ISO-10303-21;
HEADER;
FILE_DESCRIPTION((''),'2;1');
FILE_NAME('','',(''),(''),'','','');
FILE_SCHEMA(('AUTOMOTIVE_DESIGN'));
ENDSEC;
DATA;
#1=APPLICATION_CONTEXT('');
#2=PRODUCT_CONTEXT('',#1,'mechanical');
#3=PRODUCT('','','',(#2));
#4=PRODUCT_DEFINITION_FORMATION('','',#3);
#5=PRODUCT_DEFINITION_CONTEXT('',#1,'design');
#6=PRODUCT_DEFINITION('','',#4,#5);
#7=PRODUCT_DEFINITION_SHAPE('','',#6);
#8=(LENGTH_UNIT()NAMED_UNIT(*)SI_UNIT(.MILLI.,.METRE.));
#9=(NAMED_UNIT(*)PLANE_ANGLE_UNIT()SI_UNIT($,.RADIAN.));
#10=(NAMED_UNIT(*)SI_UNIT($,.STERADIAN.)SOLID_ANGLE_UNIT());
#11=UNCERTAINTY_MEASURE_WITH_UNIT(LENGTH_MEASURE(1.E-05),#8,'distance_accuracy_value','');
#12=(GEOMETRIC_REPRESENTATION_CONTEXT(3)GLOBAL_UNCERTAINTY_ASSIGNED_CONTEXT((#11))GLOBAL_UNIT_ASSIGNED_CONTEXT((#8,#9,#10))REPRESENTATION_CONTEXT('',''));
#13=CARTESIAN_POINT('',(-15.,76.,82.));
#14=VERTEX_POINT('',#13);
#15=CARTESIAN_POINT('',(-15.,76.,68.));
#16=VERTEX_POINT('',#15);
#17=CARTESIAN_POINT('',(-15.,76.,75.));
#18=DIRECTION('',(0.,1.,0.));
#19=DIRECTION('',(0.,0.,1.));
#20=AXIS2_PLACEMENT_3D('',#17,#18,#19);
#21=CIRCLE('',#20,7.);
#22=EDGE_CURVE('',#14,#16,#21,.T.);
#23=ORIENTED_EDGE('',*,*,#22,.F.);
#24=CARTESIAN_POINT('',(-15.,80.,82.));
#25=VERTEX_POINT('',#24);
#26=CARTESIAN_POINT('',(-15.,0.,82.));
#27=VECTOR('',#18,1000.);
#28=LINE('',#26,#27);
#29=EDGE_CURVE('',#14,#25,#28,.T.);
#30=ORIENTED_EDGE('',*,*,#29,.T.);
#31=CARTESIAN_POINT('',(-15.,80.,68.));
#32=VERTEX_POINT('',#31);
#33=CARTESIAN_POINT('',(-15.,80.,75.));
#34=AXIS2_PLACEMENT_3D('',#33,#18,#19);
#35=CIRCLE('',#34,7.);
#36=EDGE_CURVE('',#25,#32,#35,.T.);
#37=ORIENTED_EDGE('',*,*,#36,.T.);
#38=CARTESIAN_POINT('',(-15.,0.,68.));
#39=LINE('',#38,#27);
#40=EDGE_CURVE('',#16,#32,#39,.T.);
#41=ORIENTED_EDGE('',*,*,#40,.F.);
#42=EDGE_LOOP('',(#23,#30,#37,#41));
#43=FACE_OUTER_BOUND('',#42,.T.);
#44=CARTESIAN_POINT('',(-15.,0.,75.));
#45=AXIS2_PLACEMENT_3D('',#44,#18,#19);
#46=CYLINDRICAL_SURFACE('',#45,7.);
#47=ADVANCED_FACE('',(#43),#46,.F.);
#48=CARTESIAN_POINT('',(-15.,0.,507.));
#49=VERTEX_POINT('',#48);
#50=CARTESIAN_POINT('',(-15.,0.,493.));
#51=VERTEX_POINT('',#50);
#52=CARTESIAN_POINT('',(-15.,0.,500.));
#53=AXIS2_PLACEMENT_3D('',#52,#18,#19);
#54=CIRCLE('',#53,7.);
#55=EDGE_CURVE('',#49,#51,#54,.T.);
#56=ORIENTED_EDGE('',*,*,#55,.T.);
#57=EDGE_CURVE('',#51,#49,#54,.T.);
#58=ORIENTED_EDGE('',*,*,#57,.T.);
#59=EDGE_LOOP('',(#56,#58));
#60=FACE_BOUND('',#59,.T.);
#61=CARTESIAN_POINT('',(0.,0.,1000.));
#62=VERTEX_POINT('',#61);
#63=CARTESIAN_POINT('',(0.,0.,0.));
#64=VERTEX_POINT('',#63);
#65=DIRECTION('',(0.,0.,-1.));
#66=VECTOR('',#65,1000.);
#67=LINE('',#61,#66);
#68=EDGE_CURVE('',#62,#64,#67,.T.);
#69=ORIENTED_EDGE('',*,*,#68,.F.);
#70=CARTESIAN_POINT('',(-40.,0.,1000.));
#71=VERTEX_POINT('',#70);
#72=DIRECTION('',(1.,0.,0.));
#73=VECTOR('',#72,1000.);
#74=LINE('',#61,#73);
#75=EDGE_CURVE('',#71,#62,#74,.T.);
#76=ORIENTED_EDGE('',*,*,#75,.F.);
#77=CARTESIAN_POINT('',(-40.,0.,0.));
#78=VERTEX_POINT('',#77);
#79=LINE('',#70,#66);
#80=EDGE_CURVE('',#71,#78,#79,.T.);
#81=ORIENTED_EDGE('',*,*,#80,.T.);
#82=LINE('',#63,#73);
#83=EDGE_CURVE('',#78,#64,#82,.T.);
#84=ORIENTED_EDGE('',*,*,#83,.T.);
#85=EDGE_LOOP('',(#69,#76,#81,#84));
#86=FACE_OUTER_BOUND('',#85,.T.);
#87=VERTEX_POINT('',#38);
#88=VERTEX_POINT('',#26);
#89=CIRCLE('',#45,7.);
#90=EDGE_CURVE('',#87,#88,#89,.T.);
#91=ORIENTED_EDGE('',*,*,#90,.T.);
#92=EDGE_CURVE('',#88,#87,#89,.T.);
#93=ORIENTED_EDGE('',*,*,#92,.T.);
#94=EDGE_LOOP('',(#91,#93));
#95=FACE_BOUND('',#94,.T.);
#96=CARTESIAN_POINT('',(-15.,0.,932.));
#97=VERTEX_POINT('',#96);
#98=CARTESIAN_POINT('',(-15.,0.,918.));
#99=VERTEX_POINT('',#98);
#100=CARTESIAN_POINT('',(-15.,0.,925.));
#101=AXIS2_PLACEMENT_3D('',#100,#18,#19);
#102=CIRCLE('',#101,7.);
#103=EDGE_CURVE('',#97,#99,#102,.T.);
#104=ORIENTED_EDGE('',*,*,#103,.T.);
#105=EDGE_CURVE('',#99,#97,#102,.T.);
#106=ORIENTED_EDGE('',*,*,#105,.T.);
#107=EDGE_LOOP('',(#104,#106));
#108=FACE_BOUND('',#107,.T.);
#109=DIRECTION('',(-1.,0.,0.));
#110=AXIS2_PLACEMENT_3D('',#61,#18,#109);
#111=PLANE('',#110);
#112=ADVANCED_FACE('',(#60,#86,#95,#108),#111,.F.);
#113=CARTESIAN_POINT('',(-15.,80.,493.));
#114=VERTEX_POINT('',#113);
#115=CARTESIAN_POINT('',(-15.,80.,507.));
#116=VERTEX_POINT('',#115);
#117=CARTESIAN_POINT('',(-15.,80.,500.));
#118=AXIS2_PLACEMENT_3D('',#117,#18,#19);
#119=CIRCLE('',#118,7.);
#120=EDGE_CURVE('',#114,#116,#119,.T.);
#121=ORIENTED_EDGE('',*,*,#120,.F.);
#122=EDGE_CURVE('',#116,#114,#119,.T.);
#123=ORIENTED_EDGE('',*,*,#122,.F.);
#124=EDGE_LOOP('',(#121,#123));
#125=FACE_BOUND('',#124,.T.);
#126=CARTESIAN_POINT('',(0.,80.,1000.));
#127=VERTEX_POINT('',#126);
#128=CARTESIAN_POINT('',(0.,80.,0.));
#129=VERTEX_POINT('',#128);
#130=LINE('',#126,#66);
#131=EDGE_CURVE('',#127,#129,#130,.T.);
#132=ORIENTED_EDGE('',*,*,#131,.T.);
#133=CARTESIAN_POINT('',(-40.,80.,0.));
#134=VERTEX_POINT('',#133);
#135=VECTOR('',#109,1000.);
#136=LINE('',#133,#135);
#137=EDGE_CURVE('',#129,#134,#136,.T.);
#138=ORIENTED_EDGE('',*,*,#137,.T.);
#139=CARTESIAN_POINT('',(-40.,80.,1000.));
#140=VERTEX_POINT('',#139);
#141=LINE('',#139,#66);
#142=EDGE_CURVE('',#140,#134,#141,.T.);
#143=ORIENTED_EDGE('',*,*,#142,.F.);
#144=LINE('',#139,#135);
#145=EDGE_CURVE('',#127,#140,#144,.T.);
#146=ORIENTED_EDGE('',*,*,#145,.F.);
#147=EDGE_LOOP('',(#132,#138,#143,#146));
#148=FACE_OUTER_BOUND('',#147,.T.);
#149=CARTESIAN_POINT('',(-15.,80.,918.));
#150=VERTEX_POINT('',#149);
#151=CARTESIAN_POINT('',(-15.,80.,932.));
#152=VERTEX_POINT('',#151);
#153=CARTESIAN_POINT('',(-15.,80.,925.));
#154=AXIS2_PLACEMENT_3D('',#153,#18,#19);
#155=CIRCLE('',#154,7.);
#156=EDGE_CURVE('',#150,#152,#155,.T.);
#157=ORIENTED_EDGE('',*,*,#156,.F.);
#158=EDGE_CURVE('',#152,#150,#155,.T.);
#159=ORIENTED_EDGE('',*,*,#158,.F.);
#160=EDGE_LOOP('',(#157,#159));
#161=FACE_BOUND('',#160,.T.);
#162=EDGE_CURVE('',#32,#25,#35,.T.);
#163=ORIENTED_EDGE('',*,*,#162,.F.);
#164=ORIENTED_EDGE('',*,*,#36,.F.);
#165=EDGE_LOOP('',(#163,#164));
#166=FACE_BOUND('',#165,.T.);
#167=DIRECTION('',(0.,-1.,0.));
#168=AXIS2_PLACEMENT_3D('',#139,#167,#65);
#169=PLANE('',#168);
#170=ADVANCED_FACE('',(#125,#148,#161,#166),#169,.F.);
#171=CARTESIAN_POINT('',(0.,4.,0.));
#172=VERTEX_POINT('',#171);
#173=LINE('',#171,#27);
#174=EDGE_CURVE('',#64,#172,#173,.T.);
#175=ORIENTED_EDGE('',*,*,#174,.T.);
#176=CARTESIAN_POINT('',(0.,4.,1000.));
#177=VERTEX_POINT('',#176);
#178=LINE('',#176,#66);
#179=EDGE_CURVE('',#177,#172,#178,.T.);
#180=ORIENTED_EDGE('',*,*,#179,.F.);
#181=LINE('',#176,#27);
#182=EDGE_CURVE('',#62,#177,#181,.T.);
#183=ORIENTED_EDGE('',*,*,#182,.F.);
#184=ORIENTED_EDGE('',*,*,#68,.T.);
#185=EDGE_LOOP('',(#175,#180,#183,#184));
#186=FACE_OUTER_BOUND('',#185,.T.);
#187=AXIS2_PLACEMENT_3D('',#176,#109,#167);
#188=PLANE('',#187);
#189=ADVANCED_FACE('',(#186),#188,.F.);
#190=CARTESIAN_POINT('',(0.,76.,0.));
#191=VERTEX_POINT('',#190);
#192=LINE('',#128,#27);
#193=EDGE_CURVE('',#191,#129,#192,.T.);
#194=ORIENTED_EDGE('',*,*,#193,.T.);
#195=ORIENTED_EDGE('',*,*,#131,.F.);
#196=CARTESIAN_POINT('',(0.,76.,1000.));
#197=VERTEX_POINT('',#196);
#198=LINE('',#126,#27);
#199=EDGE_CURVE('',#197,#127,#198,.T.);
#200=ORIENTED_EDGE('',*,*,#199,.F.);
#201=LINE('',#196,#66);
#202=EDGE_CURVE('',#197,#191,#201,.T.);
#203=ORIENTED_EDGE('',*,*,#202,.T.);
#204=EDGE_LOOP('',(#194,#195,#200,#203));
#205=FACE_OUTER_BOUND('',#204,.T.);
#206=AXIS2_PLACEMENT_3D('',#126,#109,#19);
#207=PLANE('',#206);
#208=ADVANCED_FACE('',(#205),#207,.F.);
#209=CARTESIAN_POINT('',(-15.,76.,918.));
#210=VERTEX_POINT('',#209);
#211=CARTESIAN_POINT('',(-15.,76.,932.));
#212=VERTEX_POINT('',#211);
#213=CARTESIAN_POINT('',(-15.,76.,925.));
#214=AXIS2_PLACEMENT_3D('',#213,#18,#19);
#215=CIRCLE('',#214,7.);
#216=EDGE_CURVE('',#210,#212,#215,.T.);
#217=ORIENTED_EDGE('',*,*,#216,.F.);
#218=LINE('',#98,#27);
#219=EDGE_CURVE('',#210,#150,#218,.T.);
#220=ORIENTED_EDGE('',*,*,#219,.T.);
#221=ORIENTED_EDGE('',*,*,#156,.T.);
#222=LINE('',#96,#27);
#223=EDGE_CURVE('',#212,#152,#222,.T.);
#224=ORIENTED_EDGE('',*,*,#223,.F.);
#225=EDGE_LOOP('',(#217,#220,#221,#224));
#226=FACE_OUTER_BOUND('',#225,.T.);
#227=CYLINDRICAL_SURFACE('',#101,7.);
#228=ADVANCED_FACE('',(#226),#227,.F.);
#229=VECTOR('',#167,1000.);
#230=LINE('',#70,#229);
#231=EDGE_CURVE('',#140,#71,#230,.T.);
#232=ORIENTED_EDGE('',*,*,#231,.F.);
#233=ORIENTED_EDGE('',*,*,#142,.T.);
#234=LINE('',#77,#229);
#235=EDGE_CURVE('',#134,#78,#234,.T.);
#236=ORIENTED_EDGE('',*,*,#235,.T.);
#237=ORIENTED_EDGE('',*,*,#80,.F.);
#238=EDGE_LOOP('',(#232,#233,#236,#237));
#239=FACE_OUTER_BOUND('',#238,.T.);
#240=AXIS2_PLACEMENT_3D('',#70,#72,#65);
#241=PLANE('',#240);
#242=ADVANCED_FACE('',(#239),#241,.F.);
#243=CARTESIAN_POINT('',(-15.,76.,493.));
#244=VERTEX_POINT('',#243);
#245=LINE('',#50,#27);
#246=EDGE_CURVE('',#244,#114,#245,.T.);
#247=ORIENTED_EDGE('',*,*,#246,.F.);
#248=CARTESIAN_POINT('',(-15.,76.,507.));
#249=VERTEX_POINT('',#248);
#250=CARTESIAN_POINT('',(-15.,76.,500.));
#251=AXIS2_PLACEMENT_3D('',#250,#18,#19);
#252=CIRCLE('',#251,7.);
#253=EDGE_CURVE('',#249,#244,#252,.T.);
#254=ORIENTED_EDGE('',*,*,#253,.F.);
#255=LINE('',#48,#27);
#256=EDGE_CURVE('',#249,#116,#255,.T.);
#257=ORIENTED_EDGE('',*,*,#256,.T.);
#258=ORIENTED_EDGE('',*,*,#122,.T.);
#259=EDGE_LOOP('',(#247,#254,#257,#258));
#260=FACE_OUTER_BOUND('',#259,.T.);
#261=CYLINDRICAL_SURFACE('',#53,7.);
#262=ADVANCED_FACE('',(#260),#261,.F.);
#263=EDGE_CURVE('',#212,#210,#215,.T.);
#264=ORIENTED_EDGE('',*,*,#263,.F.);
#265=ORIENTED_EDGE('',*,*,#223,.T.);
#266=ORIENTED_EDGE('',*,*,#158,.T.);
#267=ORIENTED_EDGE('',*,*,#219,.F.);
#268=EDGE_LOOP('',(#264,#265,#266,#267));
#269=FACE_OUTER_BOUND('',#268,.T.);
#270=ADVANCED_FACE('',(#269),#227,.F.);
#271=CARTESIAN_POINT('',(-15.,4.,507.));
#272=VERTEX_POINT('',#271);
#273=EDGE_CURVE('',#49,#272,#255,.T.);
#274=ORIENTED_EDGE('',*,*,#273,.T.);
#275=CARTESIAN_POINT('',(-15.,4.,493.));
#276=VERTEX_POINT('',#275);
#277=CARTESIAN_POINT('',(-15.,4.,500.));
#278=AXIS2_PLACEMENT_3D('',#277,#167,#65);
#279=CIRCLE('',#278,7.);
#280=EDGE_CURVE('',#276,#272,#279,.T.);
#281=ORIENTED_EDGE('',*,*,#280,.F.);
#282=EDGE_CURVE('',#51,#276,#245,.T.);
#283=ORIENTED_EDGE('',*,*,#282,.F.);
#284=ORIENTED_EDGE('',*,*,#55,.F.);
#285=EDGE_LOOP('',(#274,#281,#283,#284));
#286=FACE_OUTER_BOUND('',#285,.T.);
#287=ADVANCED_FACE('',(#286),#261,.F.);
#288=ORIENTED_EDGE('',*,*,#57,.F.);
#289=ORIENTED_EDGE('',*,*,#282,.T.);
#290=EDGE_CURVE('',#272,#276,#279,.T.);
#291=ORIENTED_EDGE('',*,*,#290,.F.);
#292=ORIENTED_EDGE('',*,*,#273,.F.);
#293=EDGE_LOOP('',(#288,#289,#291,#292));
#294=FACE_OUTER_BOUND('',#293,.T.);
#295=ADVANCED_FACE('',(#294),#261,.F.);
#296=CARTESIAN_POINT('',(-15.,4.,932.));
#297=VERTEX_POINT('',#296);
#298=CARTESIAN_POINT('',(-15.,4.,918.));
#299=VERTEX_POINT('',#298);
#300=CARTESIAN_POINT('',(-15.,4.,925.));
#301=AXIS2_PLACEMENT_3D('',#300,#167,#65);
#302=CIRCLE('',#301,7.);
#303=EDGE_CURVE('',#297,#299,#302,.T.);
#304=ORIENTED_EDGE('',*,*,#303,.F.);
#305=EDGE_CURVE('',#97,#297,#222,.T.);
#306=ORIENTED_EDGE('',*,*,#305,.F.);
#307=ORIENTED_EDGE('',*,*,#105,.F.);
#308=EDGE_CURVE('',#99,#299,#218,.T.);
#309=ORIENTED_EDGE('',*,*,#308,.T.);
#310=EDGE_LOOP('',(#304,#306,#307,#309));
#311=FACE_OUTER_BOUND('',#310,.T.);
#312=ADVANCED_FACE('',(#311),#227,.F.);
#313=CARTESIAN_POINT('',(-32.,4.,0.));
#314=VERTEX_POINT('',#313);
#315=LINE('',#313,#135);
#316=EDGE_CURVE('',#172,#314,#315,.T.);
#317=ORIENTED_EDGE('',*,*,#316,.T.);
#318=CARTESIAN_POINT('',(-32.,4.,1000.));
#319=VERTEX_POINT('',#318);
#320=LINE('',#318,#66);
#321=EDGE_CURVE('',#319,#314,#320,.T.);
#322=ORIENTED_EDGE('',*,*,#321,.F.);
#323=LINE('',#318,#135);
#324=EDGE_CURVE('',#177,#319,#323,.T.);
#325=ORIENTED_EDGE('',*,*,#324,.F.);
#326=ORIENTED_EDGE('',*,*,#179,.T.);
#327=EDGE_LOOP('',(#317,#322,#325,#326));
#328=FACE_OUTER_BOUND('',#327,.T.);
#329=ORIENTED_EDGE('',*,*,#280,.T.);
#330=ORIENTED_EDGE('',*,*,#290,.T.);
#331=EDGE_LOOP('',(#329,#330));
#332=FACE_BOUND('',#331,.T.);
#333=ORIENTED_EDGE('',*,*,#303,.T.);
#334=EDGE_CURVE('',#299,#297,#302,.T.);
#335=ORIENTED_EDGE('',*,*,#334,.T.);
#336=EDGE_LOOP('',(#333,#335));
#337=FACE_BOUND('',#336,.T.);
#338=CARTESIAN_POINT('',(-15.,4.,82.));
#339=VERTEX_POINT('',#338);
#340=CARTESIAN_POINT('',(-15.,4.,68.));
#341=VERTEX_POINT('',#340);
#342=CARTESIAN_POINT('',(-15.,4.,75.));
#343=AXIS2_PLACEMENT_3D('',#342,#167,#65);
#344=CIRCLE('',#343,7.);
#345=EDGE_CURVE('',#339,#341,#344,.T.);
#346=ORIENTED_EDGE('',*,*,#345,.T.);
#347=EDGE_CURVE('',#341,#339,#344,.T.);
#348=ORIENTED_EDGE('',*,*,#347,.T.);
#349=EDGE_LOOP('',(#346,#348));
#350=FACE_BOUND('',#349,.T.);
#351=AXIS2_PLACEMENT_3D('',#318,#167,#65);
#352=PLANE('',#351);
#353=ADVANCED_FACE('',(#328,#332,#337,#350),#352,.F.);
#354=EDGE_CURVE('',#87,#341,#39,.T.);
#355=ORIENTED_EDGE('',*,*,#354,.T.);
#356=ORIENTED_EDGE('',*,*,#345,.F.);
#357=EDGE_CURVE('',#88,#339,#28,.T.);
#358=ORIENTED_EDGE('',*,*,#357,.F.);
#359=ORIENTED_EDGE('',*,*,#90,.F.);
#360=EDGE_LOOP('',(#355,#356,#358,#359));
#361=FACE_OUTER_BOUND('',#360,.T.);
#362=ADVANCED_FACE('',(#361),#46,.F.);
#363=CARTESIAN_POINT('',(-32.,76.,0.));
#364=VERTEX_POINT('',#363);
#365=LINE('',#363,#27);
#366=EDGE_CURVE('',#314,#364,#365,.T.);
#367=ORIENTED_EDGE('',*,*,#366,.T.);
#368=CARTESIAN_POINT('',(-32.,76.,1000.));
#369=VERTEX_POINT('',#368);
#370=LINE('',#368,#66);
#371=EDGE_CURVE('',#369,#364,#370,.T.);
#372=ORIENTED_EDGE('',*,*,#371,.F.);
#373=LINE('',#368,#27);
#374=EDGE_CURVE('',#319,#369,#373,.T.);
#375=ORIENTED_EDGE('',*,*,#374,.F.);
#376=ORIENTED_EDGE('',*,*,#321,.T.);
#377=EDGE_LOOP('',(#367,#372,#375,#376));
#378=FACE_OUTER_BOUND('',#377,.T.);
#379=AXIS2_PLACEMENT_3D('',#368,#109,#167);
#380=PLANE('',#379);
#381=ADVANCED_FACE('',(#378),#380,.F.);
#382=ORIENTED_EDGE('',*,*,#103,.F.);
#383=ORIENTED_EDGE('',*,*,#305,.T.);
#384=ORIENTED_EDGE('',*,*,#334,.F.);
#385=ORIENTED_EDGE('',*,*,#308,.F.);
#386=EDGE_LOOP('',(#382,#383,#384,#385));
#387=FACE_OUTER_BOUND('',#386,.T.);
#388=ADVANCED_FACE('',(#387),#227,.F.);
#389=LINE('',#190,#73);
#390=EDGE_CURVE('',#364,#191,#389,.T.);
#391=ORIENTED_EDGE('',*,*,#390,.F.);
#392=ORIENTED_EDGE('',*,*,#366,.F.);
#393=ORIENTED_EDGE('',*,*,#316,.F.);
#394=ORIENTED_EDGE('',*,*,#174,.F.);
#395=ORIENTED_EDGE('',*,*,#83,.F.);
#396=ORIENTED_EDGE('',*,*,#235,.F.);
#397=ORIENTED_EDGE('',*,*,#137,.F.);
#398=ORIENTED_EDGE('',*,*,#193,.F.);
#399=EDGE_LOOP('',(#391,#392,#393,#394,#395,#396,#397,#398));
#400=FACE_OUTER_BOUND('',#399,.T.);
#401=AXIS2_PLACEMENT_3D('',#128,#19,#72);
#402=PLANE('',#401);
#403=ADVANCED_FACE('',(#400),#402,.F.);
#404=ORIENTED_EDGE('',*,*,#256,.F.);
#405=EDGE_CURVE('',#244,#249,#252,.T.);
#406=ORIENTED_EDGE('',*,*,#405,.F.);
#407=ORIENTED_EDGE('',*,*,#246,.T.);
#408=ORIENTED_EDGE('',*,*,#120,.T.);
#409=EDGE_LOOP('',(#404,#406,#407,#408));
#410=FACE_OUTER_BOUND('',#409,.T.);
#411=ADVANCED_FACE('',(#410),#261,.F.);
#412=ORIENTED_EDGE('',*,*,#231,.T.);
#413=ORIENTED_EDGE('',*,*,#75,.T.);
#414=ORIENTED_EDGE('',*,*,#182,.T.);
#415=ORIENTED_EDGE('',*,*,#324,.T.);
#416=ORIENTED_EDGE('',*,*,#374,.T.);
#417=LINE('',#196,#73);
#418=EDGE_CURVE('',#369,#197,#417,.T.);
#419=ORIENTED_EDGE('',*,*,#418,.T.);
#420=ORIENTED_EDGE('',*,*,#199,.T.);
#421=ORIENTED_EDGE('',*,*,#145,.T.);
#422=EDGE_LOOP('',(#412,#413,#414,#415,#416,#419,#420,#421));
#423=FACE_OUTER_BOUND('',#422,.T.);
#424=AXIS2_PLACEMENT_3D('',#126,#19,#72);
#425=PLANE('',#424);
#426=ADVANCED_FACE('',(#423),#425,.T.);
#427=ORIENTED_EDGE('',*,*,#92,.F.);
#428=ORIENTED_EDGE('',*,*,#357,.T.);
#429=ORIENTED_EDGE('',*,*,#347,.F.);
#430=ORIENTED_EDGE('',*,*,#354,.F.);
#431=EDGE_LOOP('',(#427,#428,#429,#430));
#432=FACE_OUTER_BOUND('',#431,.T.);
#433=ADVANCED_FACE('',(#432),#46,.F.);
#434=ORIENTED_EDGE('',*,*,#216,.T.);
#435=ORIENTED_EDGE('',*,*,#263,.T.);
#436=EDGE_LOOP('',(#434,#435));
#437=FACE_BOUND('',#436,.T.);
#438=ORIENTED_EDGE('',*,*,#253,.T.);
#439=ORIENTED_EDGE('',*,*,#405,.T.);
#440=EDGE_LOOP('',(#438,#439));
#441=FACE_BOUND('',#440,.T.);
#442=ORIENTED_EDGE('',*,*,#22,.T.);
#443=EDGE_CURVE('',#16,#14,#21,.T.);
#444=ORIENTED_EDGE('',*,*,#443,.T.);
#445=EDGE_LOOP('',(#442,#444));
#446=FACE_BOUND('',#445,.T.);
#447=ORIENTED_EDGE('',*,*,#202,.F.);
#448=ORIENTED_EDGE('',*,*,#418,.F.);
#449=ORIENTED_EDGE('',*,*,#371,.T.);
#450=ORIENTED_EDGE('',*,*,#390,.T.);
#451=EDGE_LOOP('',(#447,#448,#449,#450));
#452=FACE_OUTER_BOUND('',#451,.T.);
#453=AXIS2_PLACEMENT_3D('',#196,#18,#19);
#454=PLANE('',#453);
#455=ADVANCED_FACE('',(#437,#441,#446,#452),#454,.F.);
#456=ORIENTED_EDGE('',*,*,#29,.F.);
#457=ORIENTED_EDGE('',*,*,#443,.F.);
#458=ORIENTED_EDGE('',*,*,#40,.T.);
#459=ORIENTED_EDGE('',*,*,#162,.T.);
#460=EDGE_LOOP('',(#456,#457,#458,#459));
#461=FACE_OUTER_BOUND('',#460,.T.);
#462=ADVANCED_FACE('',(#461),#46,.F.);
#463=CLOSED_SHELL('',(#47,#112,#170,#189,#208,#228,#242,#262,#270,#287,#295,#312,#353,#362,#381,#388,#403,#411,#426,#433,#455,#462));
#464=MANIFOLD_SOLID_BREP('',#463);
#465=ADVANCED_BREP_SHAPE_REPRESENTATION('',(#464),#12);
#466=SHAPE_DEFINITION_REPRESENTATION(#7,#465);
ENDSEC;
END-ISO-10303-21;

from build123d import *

# Parameters (mm, degrees)
EXTRUDE1_DEPTH     = 1000
SKETCH2_R          = 7
CUT_EXTRUDE1_DEPTH = 1004.992031841
LPATTERN1_COUNT    = 3
LPATTERN1_PITCH    = 425


with BuildPart() as part:
    # Sketch1 → Extrude1 (new body)
    with BuildSketch(Plane.XY):
        Polygon((0, 0), (-40, 0), (-40, 80), (0, 80), (0, 76), (-32, 76), (-32, 4), (0, 4), align=None)
    extrude(amount=EXTRUDE1_DEPTH)

    # Sketch2 → Cut-Extrude1 (cut, through all)
    with BuildSketch(Plane(origin=(0, 80, 0), x_dir=(1, 0, 0), z_dir=(0, 1, 0))):
        with Locations(Location((-15, -925, 0), (0, 0, 270))):
            Circle(SKETCH2_R)
    cut_extrude1 = extrude(amount=-CUT_EXTRUDE1_DEPTH, mode=Mode.SUBTRACT)

    # LPattern1: Cut-Extrude1 ×3
    with Locations(*[(0, 0, -i * LPATTERN1_PITCH) for i in range(1, LPATTERN1_COUNT)]):
        add(cut_extrude1, mode=Mode.SUBTRACT)


solid = part.part
